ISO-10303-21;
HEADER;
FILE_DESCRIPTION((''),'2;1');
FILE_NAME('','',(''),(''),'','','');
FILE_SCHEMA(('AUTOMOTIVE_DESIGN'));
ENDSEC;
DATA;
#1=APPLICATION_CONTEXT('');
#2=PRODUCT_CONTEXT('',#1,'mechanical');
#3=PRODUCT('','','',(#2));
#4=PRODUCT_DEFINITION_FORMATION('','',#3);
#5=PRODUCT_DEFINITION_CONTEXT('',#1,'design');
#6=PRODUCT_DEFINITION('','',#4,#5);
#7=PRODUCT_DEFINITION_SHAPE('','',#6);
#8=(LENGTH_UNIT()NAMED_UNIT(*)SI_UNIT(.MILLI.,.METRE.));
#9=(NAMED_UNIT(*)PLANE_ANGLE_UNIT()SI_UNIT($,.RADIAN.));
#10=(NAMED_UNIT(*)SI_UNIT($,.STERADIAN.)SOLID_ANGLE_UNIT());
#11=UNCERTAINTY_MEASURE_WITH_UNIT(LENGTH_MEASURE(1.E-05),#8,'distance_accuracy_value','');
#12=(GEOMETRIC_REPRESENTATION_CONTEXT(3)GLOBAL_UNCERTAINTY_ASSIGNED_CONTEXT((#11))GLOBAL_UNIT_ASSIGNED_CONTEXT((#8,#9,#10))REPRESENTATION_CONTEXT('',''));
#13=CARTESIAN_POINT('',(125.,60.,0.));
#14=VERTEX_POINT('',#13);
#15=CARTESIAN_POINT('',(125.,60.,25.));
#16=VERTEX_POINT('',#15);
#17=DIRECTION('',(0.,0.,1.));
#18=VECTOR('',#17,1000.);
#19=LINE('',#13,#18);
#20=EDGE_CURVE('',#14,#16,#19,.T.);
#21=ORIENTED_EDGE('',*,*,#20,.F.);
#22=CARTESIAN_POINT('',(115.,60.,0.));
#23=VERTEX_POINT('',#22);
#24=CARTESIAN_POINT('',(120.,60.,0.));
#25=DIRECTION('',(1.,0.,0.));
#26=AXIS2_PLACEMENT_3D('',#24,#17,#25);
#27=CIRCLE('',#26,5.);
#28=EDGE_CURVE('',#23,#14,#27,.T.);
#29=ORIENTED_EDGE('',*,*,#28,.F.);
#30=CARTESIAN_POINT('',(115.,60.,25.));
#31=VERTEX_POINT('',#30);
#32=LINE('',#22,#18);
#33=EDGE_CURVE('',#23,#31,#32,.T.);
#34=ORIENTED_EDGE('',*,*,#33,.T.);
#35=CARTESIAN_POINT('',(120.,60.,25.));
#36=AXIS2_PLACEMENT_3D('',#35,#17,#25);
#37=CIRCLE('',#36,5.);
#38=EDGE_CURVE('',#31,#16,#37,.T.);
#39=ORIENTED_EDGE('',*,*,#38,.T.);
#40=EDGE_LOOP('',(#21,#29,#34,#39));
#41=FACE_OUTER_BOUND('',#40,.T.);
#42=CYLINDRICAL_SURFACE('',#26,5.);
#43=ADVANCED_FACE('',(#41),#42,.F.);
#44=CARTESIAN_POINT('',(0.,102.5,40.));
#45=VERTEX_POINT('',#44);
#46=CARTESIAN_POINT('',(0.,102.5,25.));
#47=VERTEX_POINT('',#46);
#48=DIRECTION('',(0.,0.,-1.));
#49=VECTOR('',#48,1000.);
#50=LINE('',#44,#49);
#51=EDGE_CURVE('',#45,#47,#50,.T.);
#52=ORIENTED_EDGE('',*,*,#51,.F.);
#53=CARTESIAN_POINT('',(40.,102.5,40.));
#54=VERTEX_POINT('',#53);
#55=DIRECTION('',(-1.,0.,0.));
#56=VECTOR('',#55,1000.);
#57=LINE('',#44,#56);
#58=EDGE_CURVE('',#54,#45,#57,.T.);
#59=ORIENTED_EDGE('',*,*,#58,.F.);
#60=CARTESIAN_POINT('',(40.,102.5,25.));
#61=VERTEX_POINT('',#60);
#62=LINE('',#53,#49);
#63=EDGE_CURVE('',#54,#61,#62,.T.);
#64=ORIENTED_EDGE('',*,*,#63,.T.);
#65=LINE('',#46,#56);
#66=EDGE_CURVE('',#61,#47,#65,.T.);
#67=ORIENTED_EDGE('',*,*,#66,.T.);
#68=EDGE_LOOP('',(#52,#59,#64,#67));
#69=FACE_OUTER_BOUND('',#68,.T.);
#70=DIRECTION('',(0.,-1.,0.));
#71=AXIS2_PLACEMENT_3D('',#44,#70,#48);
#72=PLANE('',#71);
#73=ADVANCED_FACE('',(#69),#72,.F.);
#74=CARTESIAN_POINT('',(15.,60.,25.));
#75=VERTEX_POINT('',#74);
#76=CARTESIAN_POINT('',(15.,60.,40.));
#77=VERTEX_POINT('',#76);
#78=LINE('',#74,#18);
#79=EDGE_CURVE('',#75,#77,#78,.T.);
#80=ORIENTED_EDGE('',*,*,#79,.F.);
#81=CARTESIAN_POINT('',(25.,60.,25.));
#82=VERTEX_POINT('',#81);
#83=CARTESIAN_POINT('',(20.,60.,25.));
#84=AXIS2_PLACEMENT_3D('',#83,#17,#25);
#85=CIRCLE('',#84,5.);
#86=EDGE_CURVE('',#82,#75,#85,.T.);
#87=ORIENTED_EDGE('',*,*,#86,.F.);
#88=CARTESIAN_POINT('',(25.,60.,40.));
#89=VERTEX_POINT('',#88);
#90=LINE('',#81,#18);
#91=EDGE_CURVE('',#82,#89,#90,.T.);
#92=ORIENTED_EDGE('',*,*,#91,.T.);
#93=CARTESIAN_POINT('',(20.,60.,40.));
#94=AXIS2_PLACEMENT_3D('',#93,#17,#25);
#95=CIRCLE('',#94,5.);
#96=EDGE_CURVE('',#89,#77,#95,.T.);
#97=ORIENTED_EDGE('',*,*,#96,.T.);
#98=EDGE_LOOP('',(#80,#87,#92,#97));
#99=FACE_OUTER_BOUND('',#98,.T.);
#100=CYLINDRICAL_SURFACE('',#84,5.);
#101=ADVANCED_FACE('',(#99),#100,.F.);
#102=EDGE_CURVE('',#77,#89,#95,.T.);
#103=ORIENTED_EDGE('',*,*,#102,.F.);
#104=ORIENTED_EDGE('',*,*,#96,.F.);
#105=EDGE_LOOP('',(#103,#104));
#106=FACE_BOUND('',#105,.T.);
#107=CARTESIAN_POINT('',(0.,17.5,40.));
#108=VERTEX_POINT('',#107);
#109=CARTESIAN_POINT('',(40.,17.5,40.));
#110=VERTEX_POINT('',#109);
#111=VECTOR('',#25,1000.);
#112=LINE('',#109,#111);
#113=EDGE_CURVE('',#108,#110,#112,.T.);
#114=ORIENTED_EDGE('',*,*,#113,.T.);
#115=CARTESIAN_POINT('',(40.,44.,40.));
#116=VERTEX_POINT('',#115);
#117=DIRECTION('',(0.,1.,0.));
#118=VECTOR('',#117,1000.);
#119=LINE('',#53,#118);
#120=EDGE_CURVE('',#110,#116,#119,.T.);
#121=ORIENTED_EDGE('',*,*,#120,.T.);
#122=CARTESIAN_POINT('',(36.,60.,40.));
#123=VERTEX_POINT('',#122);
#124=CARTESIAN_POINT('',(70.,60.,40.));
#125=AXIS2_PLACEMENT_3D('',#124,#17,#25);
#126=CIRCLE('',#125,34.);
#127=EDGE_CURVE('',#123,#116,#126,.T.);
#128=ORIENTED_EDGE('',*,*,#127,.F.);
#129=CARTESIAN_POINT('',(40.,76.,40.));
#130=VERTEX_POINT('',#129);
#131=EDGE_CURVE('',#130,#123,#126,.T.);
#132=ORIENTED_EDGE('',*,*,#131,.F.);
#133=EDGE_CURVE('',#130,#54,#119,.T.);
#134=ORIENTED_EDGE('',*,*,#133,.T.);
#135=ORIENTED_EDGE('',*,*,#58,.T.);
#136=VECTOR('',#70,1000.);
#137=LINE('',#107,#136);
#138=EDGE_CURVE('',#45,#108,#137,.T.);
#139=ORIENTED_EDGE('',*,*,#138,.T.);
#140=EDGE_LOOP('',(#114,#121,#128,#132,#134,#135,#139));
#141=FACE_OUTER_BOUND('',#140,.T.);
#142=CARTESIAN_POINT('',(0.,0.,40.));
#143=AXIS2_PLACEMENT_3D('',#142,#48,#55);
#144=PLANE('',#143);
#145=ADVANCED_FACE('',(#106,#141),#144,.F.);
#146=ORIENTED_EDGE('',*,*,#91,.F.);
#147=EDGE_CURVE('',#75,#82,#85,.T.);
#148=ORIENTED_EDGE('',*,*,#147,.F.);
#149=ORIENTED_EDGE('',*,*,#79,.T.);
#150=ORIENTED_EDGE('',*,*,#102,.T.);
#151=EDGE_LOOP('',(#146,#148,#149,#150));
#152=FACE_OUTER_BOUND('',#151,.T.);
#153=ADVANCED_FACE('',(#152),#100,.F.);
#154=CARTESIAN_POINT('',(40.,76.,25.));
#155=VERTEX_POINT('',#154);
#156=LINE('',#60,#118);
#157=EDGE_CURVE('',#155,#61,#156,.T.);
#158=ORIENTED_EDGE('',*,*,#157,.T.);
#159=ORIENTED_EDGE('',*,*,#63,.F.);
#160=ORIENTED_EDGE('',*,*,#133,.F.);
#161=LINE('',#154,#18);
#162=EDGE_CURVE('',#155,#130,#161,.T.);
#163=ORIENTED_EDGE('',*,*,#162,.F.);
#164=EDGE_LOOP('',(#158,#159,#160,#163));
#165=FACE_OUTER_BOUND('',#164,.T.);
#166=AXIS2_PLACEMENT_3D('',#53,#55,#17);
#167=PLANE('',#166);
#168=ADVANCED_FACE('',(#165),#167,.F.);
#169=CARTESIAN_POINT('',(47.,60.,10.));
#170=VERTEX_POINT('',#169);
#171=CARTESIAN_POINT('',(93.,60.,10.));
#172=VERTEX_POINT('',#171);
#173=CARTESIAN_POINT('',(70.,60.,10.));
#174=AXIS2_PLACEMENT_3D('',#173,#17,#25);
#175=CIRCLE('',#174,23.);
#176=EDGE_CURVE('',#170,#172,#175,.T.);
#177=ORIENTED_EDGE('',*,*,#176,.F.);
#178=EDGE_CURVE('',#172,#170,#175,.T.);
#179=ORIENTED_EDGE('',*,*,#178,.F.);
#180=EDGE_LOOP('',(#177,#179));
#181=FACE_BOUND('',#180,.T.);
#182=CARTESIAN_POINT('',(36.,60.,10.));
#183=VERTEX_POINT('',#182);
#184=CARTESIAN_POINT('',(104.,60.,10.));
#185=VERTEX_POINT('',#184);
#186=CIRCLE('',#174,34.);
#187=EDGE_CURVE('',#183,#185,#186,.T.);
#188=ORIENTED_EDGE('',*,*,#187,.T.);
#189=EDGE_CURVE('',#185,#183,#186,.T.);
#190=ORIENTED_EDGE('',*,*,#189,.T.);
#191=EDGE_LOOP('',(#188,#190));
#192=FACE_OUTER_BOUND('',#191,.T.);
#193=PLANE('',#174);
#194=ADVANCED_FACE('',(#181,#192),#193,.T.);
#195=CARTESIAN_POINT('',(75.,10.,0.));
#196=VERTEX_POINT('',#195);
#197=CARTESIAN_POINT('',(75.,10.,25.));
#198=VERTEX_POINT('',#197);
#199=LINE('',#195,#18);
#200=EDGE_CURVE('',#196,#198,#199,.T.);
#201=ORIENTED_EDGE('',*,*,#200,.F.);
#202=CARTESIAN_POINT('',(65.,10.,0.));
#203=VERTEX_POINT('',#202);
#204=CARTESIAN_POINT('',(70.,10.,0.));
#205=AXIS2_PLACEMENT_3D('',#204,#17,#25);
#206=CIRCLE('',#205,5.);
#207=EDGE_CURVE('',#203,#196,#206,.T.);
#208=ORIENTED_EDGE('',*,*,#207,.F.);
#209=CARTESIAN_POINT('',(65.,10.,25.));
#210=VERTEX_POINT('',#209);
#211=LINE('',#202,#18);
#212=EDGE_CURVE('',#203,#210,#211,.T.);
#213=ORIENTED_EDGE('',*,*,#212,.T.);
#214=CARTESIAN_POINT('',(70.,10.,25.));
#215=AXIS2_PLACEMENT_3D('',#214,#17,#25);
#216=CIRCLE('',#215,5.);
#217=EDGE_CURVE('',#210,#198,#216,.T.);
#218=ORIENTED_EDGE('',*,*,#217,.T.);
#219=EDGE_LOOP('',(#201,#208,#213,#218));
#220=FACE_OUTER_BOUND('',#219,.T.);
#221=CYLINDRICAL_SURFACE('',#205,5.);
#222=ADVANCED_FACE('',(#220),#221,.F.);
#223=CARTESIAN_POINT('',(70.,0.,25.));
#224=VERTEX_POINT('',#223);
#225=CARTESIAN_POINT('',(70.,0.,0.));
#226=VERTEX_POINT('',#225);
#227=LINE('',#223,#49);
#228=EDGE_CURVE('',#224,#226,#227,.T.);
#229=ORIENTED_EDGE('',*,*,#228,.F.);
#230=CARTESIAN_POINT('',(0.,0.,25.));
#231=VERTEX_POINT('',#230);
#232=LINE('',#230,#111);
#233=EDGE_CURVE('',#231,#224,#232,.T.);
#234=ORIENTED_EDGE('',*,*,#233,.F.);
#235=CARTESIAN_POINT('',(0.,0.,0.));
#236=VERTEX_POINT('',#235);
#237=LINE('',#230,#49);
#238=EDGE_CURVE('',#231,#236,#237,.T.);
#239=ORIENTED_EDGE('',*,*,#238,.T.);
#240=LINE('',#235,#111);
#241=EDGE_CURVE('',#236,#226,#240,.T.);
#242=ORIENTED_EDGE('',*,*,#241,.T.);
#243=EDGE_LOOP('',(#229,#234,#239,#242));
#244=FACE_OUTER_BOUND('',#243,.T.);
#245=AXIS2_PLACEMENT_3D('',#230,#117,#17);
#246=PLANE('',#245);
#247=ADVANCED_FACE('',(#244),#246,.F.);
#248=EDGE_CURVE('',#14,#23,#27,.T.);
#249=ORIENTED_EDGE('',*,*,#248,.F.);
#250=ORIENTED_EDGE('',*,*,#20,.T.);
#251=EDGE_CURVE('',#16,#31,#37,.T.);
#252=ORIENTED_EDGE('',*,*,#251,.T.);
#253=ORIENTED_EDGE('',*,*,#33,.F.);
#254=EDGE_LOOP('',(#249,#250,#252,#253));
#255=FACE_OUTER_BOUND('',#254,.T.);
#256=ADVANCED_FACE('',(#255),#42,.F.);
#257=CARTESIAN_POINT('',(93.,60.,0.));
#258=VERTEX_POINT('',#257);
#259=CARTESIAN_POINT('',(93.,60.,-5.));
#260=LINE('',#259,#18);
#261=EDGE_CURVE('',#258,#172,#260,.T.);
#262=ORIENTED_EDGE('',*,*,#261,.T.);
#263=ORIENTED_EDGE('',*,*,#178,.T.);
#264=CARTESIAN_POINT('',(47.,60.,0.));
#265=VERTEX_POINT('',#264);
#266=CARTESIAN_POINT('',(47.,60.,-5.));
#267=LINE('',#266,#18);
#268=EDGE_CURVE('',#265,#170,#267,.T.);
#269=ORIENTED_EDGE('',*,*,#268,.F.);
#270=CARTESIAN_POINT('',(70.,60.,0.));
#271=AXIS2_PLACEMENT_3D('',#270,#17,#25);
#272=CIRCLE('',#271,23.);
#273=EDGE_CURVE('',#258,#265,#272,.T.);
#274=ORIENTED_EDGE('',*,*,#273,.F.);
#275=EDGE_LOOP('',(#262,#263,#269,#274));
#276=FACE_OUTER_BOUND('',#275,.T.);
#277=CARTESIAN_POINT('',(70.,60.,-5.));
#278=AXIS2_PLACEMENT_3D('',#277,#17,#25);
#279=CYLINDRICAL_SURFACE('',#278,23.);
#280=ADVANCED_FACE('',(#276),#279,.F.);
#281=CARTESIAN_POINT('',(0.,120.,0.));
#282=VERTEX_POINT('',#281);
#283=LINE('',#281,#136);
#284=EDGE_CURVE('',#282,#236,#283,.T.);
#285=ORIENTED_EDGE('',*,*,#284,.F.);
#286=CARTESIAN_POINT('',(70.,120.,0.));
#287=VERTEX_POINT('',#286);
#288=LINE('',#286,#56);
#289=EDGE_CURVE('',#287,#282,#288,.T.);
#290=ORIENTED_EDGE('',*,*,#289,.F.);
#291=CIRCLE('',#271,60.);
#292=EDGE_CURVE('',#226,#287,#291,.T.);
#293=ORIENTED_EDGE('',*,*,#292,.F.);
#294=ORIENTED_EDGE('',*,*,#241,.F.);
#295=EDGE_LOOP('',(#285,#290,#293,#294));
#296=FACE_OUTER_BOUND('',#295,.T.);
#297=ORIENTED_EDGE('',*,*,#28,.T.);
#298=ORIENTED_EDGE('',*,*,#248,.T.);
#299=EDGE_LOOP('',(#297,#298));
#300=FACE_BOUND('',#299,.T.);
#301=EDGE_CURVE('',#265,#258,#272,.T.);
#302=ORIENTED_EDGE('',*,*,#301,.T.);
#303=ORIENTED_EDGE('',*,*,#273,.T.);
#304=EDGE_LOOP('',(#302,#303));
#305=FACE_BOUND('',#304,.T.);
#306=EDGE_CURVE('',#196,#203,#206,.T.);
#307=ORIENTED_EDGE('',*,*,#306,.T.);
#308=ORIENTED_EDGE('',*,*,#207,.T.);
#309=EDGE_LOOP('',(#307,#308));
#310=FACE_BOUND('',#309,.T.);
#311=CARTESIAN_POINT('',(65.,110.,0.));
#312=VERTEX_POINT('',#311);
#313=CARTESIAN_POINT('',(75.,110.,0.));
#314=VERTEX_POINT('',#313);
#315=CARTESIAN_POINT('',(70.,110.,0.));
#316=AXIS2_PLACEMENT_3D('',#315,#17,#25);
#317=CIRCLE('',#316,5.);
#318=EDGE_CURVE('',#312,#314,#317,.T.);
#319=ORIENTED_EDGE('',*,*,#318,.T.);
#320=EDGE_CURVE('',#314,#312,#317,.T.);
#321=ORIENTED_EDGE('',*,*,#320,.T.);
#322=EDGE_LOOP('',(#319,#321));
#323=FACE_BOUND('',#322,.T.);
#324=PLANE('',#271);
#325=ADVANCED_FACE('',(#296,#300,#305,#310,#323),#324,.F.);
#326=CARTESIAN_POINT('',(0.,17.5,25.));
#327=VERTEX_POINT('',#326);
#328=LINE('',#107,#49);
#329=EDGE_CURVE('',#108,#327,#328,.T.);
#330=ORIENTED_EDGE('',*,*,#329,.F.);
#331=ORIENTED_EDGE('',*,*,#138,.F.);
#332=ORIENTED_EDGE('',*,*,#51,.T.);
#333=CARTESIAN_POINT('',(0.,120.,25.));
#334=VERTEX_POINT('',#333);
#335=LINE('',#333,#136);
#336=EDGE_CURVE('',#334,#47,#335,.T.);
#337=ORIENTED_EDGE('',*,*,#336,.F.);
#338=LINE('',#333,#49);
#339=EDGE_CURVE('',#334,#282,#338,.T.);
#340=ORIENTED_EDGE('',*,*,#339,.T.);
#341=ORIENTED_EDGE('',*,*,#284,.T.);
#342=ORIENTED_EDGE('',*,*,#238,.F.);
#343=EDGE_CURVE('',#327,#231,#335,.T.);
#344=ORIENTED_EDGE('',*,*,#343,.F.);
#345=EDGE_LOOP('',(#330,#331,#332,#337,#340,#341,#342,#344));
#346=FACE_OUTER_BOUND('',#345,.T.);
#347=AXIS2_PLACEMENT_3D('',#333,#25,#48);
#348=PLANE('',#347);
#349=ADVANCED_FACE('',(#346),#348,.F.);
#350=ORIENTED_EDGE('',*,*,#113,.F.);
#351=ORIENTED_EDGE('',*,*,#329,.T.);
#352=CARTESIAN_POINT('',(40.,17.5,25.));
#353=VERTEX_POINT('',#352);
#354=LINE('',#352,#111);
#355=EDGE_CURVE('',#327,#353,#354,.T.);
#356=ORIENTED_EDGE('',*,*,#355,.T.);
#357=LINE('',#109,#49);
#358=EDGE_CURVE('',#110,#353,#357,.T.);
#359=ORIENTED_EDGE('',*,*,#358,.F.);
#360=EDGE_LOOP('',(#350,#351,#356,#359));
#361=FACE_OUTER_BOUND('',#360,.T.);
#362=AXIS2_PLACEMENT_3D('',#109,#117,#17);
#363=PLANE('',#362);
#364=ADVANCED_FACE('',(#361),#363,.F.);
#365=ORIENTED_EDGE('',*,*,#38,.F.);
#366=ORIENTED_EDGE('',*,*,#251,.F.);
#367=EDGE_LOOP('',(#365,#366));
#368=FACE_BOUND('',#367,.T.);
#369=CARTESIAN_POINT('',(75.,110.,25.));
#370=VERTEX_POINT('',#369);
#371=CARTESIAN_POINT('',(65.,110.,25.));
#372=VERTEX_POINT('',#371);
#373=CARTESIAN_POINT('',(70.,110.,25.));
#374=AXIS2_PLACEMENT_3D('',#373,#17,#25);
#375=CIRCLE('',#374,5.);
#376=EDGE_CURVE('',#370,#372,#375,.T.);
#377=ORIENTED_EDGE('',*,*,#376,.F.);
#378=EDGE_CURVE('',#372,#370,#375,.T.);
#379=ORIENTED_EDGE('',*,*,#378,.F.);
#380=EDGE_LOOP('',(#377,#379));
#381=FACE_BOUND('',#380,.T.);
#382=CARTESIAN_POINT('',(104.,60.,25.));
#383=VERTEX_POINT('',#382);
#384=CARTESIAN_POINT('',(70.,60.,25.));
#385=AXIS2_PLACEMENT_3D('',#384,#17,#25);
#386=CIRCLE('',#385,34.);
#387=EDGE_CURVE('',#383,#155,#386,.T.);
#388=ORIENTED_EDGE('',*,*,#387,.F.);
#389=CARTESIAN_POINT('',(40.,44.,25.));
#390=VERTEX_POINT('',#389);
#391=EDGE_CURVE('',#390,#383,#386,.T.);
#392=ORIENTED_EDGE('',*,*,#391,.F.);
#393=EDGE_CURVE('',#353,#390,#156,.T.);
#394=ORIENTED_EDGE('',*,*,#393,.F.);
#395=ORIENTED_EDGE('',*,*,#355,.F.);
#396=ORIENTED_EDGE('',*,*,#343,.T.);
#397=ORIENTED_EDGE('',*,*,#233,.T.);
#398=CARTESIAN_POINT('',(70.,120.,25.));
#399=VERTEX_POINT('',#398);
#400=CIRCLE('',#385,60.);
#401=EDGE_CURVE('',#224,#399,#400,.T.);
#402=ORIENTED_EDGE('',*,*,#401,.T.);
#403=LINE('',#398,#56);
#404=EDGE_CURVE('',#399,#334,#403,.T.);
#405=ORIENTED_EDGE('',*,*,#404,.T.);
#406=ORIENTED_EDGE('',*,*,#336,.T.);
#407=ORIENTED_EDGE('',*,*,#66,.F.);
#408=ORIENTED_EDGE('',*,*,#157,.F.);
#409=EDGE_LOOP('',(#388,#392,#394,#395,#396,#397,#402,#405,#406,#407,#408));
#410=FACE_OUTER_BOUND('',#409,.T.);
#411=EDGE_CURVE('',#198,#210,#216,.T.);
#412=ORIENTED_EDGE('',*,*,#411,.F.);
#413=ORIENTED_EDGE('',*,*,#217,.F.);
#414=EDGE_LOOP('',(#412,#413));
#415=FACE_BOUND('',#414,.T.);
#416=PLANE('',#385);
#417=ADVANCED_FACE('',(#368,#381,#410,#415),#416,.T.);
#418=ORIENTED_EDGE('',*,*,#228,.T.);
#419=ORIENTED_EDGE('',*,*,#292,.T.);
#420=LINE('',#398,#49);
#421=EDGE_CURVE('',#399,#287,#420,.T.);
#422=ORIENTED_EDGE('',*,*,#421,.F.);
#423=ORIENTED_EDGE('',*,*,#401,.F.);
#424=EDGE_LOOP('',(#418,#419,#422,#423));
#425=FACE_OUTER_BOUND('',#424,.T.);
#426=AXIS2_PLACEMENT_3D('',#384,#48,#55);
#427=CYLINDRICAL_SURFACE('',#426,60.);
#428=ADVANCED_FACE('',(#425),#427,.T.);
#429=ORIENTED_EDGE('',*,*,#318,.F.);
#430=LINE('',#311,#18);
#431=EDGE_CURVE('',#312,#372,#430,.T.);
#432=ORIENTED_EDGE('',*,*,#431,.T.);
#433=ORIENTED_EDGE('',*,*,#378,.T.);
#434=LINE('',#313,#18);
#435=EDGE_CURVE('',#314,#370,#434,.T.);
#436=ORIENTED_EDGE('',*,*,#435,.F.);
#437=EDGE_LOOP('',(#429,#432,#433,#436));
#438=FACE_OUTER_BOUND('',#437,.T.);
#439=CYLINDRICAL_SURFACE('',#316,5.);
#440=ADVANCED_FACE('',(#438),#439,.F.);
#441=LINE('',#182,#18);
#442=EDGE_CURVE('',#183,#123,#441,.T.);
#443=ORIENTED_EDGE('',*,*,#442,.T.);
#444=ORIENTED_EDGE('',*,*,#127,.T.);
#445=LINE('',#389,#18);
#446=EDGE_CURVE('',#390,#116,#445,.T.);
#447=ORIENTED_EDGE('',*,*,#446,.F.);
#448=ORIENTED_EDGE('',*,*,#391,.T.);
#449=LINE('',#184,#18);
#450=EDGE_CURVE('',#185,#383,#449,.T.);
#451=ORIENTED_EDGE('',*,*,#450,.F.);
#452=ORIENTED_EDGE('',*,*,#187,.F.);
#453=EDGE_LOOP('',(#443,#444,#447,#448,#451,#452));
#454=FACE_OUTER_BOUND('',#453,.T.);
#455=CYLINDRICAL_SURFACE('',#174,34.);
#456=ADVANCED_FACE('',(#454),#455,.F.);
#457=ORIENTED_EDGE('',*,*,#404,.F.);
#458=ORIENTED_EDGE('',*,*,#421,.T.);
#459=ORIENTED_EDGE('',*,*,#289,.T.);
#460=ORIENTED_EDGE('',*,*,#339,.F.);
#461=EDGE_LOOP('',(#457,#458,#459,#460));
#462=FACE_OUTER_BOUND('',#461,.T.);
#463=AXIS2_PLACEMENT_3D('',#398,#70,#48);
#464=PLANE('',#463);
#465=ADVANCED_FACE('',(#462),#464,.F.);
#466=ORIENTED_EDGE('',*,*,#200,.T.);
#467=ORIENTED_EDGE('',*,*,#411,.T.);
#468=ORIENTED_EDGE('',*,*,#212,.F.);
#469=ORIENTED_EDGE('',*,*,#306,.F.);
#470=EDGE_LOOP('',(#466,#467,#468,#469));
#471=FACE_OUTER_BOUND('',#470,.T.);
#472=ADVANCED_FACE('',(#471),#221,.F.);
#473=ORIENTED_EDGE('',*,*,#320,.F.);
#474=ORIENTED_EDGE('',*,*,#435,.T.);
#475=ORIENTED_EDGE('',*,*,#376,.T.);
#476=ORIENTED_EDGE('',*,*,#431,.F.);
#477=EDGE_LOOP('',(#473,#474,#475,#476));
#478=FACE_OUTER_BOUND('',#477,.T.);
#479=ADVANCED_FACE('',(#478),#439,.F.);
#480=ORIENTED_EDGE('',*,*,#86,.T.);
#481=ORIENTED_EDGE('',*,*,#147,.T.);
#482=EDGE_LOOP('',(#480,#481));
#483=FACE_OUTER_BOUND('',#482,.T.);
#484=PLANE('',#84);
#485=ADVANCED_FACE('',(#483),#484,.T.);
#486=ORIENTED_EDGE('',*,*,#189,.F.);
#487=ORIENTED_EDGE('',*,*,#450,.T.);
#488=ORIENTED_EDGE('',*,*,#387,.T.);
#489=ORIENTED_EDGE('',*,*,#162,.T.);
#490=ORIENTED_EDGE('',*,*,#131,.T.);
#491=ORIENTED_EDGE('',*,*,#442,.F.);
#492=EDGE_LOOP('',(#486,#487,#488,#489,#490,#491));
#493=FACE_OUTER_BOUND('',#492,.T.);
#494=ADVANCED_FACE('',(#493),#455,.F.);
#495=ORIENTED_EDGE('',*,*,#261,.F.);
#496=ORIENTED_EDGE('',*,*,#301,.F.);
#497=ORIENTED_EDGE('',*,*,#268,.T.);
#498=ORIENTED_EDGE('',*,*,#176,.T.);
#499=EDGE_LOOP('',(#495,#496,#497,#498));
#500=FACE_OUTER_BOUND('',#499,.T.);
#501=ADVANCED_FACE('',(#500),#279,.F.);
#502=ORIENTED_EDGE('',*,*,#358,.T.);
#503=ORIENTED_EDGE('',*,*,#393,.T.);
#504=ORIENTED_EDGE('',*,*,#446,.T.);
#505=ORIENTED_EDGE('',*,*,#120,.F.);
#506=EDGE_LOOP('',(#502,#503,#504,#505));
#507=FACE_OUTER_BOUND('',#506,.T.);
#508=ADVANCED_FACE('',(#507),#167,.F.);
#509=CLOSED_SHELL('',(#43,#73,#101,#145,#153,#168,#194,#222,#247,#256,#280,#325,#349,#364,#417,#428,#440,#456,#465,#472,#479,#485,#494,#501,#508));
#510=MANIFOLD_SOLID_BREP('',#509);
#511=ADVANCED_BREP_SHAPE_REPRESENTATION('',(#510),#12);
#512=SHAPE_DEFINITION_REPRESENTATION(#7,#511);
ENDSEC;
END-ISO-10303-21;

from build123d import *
from build123d.topology import SkipClean

# Parameters (mm, degrees)
BASE_PLATE_DEPTH           = 25
SIDE_BLOCK_SKETCH_W        = 40
SIDE_BLOCK_SKETCH_H        = 85
SIDE_BLOCK_DEPTH           = 15
COUNTERBORE_68_SKETCH_R    = 34
COUNTERBORE_68_DEPTH       = 15
BLOCK_RELIEF_68_DEPTH      = 15
BORE_46_SKETCH_R           = 23
BORE_46_DEPTH              = 15
BLOCK_HOLE_10_SKETCH_R     = 5
BLOCK_HOLE_10_DEPTH        = 15
MOUNTING_HOLES_SKETCH_R    = 5
MOUNTING_HOLES_3X_10_DEPTH = 25


with BuildPart() as part:
    # Base Plate Sketch → Base Plate (new body)
    with BuildSketch(Plane.XY):
        with BuildLine():
            Line((0, 0), (70, 0))
            ThreePointArc((70, 0), (130, 60), (70, 120))
            Line((70, 120), (0, 120))
            Line((0, 120), (0, 0))
        make_face()
    extrude(amount=BASE_PLATE_DEPTH)

    # Side Block Sketch → Side Block (add)
    with BuildSketch(Plane.XY.offset(25)):
        with Locations((20, 60)):
            Rectangle(SIDE_BLOCK_SKETCH_W, SIDE_BLOCK_SKETCH_H)
    extrude(amount=SIDE_BLOCK_DEPTH)

    # Counterbore Ø68 Sketch → Counterbore Ø68 (cut)
    with BuildSketch(Plane.XY.offset(25)):
        with Locations((70, 60)):
            Circle(COUNTERBORE_68_SKETCH_R)
    extrude(amount=-COUNTERBORE_68_DEPTH, mode=Mode.SUBTRACT)

    # Block Relief Ø68 Sketch → Block Relief Ø68 (cut)
    with SkipClean():  # the faces are left unmerged after this step: merging them gives an invalid solid
        with BuildSketch(Plane.XY.offset(40)):
            with BuildLine():
                Line((40, 76), (40, 44))
                ThreePointArc((40, 44), (36, 60), (40, 76))
            make_face()
        extrude(amount=-BLOCK_RELIEF_68_DEPTH, mode=Mode.SUBTRACT)

    # Bore Ø46 Sketch → Bore Ø46 (cut)
    with SkipClean():  # the faces are left unmerged after this step: merging them gives an invalid solid
        with BuildSketch(Plane.XY.offset(10)):
            with Locations((70, 60)):
                Circle(BORE_46_SKETCH_R)
        extrude(amount=-BORE_46_DEPTH, mode=Mode.SUBTRACT)

    # Block Hole Ø10 Sketch → Block Hole Ø10 (cut)
    with SkipClean():  # the faces are left unmerged after this step: merging them gives an invalid solid
        with BuildSketch(Plane.XY.offset(40)):
            with Locations((20, 60)):
                Circle(BLOCK_HOLE_10_SKETCH_R)
        extrude(amount=-BLOCK_HOLE_10_DEPTH, mode=Mode.SUBTRACT)

    # Mounting Holes Sketch → Mounting Holes 3xØ10 (cut)
    with SkipClean():  # the faces are left unmerged after this step: merging them gives an invalid solid
        with BuildSketch(Plane.XY.offset(25)):
            with Locations((70, 110)):
                Circle(MOUNTING_HOLES_SKETCH_R)
            with Locations((120, 60)):
                Circle(MOUNTING_HOLES_SKETCH_R)
            with Locations((70, 10)):
                Circle(MOUNTING_HOLES_SKETCH_R)
        extrude(amount=-MOUNTING_HOLES_3X_10_DEPTH, mode=Mode.SUBTRACT)


solid = part.part
